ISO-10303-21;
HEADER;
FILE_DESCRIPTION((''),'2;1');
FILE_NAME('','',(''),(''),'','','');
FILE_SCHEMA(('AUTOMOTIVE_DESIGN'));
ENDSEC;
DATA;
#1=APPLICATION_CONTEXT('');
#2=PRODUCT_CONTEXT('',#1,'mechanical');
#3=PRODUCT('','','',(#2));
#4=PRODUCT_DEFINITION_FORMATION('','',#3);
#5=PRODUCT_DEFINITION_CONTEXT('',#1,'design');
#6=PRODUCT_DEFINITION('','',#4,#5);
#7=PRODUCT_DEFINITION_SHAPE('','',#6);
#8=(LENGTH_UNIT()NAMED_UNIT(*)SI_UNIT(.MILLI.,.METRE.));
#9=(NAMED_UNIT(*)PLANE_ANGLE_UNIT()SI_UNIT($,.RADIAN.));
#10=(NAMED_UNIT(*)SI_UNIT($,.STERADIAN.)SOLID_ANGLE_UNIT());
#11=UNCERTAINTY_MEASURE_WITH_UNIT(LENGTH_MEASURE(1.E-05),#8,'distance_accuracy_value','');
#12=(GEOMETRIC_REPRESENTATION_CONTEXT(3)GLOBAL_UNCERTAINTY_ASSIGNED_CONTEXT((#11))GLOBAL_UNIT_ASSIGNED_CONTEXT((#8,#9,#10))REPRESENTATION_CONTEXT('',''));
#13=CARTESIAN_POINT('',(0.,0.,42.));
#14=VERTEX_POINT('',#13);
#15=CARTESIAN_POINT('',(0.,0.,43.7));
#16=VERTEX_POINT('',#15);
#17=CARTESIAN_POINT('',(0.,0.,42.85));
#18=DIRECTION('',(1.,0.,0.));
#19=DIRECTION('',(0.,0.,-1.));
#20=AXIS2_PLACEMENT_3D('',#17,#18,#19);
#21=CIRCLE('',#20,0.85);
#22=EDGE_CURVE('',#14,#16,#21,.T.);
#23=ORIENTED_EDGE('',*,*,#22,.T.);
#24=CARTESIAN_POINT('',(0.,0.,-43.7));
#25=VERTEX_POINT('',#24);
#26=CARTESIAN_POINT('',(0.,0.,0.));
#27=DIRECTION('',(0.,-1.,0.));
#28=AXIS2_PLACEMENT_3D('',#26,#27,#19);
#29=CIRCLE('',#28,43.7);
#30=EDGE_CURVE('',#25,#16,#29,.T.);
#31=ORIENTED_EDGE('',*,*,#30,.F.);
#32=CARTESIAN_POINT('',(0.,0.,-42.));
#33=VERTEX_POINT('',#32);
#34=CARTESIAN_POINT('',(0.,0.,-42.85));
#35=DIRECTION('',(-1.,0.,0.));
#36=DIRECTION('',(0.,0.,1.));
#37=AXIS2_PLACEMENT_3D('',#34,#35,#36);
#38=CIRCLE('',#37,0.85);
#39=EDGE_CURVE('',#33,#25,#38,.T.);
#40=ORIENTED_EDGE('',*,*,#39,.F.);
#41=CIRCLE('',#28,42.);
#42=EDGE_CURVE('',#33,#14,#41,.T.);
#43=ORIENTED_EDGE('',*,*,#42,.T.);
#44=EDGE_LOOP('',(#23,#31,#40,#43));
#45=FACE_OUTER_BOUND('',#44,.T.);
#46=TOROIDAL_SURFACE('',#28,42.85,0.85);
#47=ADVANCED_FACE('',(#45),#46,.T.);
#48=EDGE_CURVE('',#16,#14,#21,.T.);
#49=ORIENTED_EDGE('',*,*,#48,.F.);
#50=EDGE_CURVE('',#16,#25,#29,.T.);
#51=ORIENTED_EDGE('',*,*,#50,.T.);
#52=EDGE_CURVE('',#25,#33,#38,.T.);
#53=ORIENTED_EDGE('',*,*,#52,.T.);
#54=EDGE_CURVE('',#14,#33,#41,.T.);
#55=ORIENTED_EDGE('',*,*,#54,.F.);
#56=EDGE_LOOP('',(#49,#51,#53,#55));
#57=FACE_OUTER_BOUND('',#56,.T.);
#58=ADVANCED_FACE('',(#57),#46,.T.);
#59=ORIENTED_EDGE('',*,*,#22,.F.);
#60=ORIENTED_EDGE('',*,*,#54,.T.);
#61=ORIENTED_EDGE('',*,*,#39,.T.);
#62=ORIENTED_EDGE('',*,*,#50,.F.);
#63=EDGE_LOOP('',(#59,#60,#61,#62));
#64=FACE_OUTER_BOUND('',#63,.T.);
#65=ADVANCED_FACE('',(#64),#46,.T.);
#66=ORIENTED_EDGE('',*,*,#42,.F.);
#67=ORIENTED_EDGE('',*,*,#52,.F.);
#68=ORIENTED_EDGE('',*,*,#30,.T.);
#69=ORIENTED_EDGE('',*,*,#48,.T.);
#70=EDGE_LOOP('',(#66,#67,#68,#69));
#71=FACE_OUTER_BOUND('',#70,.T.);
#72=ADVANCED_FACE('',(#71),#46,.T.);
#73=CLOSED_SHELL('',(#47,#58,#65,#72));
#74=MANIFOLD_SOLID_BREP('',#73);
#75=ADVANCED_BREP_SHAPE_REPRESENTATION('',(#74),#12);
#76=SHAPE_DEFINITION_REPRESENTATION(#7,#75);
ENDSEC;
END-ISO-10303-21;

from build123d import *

# Parameters (mm, degrees)
SKETCH1_R = 0.85


with BuildPart() as part:
    # Sketch1 → Revolve1 (revolve)
    with BuildSketch(Plane.XY, mode=Mode.PRIVATE) as revolve1_sk:
        with Locations((-42.85, 0)):
            Circle(SKETCH1_R)
    revolve(revolve1_sk.sketch.rotate(Axis((0, 0, 0), (0, 1, 0)), 270), axis=Axis((0, 0, 0), (0, 1, 0)))


solid = part.part
